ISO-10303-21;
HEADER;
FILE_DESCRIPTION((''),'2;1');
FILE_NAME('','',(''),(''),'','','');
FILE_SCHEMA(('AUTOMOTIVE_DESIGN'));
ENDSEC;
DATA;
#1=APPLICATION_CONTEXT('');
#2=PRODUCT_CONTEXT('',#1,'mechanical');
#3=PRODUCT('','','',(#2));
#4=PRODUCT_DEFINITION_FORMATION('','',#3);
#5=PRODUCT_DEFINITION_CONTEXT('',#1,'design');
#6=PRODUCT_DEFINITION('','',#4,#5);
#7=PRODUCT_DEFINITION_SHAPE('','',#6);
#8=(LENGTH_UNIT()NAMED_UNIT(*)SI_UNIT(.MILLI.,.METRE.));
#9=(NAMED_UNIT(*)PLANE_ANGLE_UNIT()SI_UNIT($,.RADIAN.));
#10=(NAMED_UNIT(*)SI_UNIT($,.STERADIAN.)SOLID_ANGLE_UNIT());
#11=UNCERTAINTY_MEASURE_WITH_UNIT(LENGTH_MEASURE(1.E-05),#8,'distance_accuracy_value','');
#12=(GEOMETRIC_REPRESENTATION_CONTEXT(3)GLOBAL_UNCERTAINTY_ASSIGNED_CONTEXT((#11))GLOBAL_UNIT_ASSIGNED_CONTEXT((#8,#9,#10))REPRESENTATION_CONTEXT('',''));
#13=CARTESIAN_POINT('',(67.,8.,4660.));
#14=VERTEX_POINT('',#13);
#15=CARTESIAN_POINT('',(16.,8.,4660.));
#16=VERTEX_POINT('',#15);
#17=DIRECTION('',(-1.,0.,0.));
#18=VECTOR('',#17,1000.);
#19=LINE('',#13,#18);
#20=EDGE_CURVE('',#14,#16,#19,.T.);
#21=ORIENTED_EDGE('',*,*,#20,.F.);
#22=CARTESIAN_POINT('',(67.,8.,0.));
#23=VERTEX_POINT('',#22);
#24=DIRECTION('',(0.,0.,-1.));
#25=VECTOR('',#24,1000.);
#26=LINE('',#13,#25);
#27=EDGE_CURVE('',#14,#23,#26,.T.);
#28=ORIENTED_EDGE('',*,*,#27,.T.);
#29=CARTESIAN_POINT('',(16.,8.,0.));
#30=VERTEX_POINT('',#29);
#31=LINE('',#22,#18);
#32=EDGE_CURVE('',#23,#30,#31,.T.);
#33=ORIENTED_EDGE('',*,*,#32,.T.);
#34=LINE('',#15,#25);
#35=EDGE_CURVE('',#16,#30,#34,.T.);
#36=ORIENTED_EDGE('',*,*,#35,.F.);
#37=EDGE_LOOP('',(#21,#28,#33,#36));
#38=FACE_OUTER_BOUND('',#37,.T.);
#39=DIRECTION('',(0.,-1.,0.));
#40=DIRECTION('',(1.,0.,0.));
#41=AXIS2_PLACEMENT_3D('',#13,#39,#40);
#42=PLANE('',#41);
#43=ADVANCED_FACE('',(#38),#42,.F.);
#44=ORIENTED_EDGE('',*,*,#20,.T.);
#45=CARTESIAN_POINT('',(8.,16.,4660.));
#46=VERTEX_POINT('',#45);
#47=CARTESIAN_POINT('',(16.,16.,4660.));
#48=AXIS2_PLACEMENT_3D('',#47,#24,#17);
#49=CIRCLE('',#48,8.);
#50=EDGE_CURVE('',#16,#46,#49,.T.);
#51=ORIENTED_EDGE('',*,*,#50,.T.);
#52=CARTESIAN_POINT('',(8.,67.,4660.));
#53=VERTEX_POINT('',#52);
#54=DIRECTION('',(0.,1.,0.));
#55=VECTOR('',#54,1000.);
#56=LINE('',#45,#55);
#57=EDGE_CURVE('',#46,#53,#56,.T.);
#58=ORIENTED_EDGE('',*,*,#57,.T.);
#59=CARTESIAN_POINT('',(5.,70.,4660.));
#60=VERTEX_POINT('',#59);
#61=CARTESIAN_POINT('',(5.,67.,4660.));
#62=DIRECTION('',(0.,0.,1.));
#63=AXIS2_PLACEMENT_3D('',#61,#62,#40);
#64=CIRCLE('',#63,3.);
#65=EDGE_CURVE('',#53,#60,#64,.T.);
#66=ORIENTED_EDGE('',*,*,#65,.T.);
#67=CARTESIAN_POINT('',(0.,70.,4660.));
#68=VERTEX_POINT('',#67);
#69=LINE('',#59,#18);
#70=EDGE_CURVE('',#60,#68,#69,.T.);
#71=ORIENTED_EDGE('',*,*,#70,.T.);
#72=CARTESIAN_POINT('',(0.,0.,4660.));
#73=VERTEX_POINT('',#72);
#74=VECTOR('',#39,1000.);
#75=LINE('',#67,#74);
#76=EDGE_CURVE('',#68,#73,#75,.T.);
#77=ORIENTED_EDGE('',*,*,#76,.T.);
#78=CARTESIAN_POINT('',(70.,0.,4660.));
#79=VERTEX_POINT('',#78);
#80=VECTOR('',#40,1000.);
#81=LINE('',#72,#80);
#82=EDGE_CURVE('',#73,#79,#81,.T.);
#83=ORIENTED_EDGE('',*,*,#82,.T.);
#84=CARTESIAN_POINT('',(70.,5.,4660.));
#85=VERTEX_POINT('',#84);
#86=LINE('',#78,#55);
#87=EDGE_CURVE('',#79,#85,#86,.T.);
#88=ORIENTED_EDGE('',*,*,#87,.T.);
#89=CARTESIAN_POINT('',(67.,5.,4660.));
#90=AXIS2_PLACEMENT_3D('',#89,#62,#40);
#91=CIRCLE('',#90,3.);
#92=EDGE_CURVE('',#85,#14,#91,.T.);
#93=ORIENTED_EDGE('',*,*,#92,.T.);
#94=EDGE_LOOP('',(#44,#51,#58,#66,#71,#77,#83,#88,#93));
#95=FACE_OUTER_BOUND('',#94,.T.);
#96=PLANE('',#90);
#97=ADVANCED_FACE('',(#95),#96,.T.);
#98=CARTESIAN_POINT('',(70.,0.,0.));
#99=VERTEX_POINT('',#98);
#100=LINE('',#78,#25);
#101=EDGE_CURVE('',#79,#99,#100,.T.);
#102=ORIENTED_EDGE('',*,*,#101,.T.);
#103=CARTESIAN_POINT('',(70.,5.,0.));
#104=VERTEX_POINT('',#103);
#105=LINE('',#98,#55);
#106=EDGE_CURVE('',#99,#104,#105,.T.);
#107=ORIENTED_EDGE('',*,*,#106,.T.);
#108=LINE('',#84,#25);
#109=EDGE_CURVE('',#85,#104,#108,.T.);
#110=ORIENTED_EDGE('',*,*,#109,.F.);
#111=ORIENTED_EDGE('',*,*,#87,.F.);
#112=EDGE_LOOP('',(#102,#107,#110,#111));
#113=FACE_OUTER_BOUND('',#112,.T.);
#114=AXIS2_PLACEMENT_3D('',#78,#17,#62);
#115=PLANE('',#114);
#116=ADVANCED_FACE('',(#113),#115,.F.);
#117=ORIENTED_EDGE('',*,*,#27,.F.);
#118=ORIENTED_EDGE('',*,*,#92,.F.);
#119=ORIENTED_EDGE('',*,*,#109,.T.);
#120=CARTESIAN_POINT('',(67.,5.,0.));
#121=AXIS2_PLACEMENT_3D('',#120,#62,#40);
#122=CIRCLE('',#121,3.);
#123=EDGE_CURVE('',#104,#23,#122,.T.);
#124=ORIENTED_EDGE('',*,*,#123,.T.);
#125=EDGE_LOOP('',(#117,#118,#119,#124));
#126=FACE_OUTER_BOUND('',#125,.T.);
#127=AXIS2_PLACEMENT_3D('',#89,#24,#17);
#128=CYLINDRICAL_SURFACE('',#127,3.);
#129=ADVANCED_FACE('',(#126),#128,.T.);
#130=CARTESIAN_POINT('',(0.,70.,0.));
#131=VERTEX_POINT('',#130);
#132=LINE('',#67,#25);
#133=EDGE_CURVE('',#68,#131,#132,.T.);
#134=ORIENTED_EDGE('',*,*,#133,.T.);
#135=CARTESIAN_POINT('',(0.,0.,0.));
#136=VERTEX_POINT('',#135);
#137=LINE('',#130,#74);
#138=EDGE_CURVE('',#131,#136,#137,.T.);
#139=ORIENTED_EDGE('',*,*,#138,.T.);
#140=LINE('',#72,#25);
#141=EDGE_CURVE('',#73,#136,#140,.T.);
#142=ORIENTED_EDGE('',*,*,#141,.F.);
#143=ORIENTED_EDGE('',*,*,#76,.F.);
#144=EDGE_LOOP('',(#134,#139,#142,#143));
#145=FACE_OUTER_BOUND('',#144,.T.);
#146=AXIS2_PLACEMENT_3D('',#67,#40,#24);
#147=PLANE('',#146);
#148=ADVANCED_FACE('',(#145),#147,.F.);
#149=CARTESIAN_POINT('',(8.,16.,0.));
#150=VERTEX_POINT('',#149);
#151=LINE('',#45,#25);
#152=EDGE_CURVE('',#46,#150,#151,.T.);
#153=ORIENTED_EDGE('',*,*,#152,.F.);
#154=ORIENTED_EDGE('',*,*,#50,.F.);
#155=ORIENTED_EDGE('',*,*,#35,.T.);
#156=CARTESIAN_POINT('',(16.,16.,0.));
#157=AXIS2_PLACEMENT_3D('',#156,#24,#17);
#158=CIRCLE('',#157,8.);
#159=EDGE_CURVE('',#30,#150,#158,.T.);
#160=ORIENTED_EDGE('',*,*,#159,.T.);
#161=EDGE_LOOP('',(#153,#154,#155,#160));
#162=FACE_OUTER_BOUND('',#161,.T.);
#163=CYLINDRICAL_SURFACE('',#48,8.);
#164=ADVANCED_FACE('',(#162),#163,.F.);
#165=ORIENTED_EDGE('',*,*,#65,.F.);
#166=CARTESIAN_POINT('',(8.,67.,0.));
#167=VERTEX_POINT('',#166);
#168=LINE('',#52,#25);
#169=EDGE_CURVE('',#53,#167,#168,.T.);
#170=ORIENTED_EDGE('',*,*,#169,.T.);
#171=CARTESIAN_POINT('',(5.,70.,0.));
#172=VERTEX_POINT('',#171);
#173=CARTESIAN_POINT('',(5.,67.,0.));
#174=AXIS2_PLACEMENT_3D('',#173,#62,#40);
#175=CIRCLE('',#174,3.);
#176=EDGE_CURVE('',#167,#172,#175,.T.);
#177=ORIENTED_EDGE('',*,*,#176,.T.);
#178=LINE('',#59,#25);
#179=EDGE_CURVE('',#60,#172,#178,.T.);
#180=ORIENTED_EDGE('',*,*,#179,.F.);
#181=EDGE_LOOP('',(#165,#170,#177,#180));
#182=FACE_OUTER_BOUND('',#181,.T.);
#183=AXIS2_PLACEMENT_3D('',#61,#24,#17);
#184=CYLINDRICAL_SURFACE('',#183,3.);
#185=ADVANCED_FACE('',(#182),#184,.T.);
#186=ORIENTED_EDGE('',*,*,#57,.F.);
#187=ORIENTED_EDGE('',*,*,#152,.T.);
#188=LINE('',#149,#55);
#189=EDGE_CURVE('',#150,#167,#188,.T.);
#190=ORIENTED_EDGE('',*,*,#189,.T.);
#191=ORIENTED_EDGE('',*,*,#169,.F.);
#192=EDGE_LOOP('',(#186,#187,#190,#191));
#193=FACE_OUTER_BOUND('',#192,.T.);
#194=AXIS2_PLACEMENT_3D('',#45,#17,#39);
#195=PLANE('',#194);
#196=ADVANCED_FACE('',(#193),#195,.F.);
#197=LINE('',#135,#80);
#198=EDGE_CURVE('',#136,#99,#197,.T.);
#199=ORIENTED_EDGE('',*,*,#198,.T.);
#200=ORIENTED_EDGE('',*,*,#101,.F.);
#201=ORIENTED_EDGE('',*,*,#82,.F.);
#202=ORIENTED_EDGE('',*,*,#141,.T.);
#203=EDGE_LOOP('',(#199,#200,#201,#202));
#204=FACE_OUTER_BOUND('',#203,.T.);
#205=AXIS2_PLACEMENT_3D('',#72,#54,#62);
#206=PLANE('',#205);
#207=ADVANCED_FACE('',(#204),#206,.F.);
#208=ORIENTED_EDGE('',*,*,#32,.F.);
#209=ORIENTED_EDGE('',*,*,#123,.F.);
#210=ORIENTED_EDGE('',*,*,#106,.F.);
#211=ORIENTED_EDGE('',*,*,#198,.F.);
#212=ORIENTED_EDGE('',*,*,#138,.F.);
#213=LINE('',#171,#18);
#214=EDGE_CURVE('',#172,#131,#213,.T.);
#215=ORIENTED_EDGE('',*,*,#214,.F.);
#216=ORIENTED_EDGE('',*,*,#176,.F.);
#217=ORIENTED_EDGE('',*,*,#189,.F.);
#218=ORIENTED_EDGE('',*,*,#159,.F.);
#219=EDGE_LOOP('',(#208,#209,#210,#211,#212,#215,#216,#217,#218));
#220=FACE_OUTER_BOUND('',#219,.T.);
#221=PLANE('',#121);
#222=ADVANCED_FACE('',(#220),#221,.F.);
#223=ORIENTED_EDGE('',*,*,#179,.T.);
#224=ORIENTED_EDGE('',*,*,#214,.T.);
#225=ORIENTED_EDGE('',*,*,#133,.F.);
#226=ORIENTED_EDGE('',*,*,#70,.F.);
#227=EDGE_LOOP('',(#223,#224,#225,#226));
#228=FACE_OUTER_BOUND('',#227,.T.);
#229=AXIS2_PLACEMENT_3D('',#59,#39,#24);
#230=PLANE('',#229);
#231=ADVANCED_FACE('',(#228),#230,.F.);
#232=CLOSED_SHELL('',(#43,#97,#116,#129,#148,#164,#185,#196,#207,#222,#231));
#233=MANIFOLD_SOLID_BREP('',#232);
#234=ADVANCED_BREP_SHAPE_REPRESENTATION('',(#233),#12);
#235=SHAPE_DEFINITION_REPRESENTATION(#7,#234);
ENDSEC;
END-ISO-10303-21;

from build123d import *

# Parameters (mm, degrees)
BOSS_EXTRUDE1_DEPTH = 4660


with BuildPart() as part:
    # Sketch1 → Boss-Extrude1 (new body)
    with BuildSketch(Plane.XY):
        with BuildLine():
            Line((0, 70), (0, 0))
            Line((0, 0), (70, 0))
            Line((70, 0), (70, 5))
            ThreePointArc((70, 5), (69.121320344, 7.121320344), (67, 8))
            Line((67, 8), (16, 8))
            ThreePointArc((16, 8), (10.343145751, 10.343145751), (8, 16))
            Line((8, 16), (8, 67))
            ThreePointArc((8, 67), (7.121320344, 69.121320344), (5, 70))
            Line((5, 70), (0, 70))
        make_face()
    extrude(amount=BOSS_EXTRUDE1_DEPTH)


solid = part.part
